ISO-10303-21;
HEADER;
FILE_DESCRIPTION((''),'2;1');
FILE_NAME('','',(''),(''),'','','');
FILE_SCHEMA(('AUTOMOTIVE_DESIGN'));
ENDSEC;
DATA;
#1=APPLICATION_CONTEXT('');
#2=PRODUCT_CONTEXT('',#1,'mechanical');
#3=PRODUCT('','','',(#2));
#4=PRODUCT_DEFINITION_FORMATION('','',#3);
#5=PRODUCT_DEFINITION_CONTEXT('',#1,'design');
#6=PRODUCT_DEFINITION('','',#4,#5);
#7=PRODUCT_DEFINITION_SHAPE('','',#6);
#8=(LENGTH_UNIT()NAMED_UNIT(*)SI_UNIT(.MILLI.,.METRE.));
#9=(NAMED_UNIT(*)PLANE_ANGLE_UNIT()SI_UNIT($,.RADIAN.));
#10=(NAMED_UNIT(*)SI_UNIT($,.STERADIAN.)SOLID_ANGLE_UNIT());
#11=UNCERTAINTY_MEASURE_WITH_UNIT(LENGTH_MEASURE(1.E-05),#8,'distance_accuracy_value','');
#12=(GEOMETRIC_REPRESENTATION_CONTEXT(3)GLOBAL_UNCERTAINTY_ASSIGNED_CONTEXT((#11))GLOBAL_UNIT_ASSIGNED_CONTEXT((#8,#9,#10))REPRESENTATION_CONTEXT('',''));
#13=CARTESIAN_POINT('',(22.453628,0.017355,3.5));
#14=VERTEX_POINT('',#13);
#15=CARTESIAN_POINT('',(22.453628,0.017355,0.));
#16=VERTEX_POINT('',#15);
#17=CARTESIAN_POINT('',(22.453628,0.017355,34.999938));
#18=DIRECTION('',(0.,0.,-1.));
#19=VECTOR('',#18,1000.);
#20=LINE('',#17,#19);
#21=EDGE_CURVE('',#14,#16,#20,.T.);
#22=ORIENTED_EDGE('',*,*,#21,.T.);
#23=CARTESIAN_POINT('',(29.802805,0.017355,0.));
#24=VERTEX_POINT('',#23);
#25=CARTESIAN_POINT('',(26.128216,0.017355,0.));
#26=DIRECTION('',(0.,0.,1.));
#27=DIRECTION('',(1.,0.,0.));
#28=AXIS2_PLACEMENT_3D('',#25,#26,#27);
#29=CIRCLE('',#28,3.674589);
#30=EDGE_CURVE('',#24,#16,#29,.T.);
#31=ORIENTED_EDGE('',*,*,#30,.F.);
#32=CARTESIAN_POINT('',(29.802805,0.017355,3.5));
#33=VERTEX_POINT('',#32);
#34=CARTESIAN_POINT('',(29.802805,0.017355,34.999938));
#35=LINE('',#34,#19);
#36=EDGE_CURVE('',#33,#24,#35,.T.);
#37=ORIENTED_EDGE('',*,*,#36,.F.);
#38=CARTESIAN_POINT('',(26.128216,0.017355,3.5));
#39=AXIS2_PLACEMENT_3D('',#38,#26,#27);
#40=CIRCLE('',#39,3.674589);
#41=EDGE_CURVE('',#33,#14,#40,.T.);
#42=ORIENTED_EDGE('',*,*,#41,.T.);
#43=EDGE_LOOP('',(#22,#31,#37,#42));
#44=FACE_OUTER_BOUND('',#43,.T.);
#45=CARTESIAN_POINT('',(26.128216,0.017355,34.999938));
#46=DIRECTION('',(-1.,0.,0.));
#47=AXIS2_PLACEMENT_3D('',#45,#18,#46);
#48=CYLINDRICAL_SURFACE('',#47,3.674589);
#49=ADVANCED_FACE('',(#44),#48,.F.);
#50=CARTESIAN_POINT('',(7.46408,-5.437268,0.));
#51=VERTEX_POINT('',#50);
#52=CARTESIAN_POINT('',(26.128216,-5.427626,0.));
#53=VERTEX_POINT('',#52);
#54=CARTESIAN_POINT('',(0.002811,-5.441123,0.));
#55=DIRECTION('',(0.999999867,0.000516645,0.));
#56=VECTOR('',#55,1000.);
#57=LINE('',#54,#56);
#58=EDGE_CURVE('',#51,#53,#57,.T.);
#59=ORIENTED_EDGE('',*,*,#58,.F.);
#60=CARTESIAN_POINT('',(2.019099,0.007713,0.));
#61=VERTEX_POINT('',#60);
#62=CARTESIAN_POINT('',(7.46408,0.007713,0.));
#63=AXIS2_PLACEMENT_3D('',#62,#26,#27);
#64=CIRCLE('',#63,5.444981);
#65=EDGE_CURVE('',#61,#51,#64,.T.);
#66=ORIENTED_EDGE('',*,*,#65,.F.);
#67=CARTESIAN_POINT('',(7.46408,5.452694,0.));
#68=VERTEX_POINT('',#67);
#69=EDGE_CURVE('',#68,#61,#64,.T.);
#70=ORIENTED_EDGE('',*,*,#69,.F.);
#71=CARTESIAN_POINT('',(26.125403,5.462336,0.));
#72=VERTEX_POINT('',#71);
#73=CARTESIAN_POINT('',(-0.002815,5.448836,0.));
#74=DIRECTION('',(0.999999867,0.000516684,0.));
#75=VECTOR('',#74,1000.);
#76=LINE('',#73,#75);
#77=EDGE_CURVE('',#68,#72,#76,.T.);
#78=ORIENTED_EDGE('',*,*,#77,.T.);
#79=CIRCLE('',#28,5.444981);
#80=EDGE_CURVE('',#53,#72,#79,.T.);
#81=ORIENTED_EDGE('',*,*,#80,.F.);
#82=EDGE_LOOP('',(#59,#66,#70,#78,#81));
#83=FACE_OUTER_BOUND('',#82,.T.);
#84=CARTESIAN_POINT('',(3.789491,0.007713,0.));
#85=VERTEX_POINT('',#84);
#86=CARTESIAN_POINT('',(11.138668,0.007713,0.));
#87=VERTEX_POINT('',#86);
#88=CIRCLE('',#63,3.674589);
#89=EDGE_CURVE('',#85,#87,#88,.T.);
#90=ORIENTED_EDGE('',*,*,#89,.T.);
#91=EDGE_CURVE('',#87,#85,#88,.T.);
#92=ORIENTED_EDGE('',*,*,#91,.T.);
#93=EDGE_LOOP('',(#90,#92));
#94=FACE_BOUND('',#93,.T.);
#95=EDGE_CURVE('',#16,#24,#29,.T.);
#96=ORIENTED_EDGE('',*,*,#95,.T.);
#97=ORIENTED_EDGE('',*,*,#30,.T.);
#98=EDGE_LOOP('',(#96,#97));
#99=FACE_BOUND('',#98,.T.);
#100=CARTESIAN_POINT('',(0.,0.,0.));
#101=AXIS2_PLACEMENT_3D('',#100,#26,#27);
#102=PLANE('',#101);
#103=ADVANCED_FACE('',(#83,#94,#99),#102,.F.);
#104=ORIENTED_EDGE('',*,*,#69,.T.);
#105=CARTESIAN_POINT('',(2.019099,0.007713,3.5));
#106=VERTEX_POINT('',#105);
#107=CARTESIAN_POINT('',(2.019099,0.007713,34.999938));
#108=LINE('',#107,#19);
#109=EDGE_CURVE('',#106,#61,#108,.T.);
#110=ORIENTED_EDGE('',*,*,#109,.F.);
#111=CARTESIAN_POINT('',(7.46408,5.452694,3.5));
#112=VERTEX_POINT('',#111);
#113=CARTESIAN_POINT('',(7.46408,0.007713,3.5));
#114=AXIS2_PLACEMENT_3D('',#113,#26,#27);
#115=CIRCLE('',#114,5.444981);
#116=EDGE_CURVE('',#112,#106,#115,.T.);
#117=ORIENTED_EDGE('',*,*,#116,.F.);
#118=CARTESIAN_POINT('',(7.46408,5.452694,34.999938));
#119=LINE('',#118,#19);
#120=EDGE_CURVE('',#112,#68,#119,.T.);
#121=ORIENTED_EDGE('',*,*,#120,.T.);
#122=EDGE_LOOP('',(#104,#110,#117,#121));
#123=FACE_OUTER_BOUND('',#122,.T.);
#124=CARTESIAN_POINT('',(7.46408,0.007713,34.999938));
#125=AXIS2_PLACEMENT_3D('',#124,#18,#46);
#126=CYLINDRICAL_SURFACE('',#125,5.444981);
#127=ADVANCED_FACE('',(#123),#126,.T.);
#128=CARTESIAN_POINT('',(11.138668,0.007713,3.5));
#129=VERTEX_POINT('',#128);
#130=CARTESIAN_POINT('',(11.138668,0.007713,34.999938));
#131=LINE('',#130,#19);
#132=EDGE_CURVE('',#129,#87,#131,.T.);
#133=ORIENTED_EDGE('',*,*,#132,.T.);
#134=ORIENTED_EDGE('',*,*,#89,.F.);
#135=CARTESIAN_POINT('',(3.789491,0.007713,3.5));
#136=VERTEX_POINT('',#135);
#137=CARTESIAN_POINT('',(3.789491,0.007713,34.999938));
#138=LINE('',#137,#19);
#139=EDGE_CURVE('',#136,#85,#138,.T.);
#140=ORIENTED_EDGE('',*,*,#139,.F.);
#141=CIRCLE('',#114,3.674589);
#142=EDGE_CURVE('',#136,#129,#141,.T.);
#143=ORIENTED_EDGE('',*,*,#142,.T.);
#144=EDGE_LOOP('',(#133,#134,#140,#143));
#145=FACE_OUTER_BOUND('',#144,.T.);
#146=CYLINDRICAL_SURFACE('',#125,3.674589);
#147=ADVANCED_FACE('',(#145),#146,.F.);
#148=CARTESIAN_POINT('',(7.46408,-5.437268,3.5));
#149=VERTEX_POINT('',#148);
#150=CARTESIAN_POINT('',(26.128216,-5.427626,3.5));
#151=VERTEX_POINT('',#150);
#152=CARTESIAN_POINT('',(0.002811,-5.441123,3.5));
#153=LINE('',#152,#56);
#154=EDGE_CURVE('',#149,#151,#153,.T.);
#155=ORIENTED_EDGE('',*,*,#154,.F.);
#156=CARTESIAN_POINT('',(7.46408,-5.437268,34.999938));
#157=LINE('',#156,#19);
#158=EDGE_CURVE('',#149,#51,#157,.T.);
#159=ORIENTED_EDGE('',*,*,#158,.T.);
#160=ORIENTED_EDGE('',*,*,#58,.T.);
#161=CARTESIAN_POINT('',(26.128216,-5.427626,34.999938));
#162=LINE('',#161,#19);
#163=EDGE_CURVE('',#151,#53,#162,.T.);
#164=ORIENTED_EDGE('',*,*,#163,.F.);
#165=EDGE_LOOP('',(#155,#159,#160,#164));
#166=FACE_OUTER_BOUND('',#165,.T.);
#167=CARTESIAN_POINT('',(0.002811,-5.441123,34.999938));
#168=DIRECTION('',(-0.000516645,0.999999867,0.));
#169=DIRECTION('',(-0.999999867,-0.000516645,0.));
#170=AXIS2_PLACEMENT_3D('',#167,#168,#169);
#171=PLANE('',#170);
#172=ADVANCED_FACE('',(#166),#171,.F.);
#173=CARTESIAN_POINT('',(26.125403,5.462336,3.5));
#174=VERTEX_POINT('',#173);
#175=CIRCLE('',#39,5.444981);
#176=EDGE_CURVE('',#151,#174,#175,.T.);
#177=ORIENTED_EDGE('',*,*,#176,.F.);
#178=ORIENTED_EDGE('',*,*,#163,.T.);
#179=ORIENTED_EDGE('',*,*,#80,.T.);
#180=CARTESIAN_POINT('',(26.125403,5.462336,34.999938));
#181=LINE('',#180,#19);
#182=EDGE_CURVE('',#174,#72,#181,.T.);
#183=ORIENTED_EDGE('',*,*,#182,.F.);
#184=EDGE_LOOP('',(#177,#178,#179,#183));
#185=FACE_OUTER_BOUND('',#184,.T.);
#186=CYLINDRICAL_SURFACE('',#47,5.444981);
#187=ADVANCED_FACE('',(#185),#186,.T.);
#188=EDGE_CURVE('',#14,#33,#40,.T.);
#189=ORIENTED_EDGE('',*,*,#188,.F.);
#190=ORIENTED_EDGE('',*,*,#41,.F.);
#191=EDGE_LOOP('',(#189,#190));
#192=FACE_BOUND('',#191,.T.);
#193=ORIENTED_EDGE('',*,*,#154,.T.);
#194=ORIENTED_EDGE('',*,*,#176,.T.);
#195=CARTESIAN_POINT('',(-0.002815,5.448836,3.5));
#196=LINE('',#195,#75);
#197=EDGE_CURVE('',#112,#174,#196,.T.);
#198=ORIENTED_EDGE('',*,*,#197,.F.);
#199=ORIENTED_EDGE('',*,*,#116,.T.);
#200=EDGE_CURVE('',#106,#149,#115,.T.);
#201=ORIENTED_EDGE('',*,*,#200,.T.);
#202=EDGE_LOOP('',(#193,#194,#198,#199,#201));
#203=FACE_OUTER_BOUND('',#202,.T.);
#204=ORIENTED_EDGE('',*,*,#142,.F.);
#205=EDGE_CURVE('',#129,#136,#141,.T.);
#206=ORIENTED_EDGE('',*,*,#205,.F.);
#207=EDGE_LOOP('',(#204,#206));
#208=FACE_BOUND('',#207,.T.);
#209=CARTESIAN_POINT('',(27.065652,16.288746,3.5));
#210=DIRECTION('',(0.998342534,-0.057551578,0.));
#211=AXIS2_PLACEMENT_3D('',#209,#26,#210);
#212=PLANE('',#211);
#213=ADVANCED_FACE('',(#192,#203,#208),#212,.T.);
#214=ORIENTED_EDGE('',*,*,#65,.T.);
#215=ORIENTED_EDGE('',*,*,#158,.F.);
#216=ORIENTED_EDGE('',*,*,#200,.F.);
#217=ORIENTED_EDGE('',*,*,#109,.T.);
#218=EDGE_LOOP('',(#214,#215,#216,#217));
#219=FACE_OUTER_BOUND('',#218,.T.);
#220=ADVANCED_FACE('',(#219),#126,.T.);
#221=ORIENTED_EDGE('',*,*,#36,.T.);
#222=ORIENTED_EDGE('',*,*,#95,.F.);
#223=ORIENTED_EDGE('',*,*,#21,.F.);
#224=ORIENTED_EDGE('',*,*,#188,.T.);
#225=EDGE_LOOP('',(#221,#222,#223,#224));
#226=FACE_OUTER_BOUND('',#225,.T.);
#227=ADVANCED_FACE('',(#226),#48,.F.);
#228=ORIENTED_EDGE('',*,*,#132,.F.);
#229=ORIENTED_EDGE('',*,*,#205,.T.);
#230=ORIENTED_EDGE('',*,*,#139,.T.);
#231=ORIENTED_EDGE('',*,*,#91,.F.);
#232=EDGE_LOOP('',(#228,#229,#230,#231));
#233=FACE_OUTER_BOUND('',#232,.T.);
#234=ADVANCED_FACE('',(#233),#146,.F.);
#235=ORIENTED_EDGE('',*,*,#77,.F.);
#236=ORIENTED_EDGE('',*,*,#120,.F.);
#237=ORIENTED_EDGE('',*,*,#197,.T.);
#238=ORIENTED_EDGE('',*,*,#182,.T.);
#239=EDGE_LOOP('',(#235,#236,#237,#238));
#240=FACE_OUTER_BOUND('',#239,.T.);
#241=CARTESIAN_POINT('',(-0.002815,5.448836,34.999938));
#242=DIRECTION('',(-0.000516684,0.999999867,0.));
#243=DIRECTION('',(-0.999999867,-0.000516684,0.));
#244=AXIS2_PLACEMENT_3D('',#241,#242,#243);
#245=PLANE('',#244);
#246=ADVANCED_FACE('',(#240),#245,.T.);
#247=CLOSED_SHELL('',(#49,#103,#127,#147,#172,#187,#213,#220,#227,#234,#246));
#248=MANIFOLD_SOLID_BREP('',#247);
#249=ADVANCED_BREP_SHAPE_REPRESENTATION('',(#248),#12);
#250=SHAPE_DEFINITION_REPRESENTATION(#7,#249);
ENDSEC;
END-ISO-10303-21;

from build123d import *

# Parameters (mm, degrees)
SKETCH1_R           = 3.674588618
BOSS_EXTRUDE1_DEPTH = 3.5


with BuildPart() as part:
    # Sketch1 → Boss-Extrude1 (new body)
    with BuildSketch(Plane.XY):
        with BuildLine():
            Line((26.125402815, 5.46233555), (7.464079644, 5.452693539))
            ThreePointArc((7.464079644, 5.452693539), (2.01909867, 0.007712565), (7.464079644, -5.43726841))
            Line((7.464079644, -5.43726841), (7.46970589, -5.437265503))
            Line((7.46970589, -5.437265503), (26.128216151, -5.427625672))
            ThreePointArc((26.128216151, -5.427625672), (31.573196944, 0.01876197), (26.125402815, 5.46233555))
        make_face()
        with Locations((7.464079644, 0.007712565)):
            Circle(SKETCH1_R, mode=Mode.SUBTRACT)
        with Locations((26.128216151, 0.017355302)):
            Circle(SKETCH1_R, mode=Mode.SUBTRACT)
    extrude(amount=BOSS_EXTRUDE1_DEPTH)


solid = part.part
